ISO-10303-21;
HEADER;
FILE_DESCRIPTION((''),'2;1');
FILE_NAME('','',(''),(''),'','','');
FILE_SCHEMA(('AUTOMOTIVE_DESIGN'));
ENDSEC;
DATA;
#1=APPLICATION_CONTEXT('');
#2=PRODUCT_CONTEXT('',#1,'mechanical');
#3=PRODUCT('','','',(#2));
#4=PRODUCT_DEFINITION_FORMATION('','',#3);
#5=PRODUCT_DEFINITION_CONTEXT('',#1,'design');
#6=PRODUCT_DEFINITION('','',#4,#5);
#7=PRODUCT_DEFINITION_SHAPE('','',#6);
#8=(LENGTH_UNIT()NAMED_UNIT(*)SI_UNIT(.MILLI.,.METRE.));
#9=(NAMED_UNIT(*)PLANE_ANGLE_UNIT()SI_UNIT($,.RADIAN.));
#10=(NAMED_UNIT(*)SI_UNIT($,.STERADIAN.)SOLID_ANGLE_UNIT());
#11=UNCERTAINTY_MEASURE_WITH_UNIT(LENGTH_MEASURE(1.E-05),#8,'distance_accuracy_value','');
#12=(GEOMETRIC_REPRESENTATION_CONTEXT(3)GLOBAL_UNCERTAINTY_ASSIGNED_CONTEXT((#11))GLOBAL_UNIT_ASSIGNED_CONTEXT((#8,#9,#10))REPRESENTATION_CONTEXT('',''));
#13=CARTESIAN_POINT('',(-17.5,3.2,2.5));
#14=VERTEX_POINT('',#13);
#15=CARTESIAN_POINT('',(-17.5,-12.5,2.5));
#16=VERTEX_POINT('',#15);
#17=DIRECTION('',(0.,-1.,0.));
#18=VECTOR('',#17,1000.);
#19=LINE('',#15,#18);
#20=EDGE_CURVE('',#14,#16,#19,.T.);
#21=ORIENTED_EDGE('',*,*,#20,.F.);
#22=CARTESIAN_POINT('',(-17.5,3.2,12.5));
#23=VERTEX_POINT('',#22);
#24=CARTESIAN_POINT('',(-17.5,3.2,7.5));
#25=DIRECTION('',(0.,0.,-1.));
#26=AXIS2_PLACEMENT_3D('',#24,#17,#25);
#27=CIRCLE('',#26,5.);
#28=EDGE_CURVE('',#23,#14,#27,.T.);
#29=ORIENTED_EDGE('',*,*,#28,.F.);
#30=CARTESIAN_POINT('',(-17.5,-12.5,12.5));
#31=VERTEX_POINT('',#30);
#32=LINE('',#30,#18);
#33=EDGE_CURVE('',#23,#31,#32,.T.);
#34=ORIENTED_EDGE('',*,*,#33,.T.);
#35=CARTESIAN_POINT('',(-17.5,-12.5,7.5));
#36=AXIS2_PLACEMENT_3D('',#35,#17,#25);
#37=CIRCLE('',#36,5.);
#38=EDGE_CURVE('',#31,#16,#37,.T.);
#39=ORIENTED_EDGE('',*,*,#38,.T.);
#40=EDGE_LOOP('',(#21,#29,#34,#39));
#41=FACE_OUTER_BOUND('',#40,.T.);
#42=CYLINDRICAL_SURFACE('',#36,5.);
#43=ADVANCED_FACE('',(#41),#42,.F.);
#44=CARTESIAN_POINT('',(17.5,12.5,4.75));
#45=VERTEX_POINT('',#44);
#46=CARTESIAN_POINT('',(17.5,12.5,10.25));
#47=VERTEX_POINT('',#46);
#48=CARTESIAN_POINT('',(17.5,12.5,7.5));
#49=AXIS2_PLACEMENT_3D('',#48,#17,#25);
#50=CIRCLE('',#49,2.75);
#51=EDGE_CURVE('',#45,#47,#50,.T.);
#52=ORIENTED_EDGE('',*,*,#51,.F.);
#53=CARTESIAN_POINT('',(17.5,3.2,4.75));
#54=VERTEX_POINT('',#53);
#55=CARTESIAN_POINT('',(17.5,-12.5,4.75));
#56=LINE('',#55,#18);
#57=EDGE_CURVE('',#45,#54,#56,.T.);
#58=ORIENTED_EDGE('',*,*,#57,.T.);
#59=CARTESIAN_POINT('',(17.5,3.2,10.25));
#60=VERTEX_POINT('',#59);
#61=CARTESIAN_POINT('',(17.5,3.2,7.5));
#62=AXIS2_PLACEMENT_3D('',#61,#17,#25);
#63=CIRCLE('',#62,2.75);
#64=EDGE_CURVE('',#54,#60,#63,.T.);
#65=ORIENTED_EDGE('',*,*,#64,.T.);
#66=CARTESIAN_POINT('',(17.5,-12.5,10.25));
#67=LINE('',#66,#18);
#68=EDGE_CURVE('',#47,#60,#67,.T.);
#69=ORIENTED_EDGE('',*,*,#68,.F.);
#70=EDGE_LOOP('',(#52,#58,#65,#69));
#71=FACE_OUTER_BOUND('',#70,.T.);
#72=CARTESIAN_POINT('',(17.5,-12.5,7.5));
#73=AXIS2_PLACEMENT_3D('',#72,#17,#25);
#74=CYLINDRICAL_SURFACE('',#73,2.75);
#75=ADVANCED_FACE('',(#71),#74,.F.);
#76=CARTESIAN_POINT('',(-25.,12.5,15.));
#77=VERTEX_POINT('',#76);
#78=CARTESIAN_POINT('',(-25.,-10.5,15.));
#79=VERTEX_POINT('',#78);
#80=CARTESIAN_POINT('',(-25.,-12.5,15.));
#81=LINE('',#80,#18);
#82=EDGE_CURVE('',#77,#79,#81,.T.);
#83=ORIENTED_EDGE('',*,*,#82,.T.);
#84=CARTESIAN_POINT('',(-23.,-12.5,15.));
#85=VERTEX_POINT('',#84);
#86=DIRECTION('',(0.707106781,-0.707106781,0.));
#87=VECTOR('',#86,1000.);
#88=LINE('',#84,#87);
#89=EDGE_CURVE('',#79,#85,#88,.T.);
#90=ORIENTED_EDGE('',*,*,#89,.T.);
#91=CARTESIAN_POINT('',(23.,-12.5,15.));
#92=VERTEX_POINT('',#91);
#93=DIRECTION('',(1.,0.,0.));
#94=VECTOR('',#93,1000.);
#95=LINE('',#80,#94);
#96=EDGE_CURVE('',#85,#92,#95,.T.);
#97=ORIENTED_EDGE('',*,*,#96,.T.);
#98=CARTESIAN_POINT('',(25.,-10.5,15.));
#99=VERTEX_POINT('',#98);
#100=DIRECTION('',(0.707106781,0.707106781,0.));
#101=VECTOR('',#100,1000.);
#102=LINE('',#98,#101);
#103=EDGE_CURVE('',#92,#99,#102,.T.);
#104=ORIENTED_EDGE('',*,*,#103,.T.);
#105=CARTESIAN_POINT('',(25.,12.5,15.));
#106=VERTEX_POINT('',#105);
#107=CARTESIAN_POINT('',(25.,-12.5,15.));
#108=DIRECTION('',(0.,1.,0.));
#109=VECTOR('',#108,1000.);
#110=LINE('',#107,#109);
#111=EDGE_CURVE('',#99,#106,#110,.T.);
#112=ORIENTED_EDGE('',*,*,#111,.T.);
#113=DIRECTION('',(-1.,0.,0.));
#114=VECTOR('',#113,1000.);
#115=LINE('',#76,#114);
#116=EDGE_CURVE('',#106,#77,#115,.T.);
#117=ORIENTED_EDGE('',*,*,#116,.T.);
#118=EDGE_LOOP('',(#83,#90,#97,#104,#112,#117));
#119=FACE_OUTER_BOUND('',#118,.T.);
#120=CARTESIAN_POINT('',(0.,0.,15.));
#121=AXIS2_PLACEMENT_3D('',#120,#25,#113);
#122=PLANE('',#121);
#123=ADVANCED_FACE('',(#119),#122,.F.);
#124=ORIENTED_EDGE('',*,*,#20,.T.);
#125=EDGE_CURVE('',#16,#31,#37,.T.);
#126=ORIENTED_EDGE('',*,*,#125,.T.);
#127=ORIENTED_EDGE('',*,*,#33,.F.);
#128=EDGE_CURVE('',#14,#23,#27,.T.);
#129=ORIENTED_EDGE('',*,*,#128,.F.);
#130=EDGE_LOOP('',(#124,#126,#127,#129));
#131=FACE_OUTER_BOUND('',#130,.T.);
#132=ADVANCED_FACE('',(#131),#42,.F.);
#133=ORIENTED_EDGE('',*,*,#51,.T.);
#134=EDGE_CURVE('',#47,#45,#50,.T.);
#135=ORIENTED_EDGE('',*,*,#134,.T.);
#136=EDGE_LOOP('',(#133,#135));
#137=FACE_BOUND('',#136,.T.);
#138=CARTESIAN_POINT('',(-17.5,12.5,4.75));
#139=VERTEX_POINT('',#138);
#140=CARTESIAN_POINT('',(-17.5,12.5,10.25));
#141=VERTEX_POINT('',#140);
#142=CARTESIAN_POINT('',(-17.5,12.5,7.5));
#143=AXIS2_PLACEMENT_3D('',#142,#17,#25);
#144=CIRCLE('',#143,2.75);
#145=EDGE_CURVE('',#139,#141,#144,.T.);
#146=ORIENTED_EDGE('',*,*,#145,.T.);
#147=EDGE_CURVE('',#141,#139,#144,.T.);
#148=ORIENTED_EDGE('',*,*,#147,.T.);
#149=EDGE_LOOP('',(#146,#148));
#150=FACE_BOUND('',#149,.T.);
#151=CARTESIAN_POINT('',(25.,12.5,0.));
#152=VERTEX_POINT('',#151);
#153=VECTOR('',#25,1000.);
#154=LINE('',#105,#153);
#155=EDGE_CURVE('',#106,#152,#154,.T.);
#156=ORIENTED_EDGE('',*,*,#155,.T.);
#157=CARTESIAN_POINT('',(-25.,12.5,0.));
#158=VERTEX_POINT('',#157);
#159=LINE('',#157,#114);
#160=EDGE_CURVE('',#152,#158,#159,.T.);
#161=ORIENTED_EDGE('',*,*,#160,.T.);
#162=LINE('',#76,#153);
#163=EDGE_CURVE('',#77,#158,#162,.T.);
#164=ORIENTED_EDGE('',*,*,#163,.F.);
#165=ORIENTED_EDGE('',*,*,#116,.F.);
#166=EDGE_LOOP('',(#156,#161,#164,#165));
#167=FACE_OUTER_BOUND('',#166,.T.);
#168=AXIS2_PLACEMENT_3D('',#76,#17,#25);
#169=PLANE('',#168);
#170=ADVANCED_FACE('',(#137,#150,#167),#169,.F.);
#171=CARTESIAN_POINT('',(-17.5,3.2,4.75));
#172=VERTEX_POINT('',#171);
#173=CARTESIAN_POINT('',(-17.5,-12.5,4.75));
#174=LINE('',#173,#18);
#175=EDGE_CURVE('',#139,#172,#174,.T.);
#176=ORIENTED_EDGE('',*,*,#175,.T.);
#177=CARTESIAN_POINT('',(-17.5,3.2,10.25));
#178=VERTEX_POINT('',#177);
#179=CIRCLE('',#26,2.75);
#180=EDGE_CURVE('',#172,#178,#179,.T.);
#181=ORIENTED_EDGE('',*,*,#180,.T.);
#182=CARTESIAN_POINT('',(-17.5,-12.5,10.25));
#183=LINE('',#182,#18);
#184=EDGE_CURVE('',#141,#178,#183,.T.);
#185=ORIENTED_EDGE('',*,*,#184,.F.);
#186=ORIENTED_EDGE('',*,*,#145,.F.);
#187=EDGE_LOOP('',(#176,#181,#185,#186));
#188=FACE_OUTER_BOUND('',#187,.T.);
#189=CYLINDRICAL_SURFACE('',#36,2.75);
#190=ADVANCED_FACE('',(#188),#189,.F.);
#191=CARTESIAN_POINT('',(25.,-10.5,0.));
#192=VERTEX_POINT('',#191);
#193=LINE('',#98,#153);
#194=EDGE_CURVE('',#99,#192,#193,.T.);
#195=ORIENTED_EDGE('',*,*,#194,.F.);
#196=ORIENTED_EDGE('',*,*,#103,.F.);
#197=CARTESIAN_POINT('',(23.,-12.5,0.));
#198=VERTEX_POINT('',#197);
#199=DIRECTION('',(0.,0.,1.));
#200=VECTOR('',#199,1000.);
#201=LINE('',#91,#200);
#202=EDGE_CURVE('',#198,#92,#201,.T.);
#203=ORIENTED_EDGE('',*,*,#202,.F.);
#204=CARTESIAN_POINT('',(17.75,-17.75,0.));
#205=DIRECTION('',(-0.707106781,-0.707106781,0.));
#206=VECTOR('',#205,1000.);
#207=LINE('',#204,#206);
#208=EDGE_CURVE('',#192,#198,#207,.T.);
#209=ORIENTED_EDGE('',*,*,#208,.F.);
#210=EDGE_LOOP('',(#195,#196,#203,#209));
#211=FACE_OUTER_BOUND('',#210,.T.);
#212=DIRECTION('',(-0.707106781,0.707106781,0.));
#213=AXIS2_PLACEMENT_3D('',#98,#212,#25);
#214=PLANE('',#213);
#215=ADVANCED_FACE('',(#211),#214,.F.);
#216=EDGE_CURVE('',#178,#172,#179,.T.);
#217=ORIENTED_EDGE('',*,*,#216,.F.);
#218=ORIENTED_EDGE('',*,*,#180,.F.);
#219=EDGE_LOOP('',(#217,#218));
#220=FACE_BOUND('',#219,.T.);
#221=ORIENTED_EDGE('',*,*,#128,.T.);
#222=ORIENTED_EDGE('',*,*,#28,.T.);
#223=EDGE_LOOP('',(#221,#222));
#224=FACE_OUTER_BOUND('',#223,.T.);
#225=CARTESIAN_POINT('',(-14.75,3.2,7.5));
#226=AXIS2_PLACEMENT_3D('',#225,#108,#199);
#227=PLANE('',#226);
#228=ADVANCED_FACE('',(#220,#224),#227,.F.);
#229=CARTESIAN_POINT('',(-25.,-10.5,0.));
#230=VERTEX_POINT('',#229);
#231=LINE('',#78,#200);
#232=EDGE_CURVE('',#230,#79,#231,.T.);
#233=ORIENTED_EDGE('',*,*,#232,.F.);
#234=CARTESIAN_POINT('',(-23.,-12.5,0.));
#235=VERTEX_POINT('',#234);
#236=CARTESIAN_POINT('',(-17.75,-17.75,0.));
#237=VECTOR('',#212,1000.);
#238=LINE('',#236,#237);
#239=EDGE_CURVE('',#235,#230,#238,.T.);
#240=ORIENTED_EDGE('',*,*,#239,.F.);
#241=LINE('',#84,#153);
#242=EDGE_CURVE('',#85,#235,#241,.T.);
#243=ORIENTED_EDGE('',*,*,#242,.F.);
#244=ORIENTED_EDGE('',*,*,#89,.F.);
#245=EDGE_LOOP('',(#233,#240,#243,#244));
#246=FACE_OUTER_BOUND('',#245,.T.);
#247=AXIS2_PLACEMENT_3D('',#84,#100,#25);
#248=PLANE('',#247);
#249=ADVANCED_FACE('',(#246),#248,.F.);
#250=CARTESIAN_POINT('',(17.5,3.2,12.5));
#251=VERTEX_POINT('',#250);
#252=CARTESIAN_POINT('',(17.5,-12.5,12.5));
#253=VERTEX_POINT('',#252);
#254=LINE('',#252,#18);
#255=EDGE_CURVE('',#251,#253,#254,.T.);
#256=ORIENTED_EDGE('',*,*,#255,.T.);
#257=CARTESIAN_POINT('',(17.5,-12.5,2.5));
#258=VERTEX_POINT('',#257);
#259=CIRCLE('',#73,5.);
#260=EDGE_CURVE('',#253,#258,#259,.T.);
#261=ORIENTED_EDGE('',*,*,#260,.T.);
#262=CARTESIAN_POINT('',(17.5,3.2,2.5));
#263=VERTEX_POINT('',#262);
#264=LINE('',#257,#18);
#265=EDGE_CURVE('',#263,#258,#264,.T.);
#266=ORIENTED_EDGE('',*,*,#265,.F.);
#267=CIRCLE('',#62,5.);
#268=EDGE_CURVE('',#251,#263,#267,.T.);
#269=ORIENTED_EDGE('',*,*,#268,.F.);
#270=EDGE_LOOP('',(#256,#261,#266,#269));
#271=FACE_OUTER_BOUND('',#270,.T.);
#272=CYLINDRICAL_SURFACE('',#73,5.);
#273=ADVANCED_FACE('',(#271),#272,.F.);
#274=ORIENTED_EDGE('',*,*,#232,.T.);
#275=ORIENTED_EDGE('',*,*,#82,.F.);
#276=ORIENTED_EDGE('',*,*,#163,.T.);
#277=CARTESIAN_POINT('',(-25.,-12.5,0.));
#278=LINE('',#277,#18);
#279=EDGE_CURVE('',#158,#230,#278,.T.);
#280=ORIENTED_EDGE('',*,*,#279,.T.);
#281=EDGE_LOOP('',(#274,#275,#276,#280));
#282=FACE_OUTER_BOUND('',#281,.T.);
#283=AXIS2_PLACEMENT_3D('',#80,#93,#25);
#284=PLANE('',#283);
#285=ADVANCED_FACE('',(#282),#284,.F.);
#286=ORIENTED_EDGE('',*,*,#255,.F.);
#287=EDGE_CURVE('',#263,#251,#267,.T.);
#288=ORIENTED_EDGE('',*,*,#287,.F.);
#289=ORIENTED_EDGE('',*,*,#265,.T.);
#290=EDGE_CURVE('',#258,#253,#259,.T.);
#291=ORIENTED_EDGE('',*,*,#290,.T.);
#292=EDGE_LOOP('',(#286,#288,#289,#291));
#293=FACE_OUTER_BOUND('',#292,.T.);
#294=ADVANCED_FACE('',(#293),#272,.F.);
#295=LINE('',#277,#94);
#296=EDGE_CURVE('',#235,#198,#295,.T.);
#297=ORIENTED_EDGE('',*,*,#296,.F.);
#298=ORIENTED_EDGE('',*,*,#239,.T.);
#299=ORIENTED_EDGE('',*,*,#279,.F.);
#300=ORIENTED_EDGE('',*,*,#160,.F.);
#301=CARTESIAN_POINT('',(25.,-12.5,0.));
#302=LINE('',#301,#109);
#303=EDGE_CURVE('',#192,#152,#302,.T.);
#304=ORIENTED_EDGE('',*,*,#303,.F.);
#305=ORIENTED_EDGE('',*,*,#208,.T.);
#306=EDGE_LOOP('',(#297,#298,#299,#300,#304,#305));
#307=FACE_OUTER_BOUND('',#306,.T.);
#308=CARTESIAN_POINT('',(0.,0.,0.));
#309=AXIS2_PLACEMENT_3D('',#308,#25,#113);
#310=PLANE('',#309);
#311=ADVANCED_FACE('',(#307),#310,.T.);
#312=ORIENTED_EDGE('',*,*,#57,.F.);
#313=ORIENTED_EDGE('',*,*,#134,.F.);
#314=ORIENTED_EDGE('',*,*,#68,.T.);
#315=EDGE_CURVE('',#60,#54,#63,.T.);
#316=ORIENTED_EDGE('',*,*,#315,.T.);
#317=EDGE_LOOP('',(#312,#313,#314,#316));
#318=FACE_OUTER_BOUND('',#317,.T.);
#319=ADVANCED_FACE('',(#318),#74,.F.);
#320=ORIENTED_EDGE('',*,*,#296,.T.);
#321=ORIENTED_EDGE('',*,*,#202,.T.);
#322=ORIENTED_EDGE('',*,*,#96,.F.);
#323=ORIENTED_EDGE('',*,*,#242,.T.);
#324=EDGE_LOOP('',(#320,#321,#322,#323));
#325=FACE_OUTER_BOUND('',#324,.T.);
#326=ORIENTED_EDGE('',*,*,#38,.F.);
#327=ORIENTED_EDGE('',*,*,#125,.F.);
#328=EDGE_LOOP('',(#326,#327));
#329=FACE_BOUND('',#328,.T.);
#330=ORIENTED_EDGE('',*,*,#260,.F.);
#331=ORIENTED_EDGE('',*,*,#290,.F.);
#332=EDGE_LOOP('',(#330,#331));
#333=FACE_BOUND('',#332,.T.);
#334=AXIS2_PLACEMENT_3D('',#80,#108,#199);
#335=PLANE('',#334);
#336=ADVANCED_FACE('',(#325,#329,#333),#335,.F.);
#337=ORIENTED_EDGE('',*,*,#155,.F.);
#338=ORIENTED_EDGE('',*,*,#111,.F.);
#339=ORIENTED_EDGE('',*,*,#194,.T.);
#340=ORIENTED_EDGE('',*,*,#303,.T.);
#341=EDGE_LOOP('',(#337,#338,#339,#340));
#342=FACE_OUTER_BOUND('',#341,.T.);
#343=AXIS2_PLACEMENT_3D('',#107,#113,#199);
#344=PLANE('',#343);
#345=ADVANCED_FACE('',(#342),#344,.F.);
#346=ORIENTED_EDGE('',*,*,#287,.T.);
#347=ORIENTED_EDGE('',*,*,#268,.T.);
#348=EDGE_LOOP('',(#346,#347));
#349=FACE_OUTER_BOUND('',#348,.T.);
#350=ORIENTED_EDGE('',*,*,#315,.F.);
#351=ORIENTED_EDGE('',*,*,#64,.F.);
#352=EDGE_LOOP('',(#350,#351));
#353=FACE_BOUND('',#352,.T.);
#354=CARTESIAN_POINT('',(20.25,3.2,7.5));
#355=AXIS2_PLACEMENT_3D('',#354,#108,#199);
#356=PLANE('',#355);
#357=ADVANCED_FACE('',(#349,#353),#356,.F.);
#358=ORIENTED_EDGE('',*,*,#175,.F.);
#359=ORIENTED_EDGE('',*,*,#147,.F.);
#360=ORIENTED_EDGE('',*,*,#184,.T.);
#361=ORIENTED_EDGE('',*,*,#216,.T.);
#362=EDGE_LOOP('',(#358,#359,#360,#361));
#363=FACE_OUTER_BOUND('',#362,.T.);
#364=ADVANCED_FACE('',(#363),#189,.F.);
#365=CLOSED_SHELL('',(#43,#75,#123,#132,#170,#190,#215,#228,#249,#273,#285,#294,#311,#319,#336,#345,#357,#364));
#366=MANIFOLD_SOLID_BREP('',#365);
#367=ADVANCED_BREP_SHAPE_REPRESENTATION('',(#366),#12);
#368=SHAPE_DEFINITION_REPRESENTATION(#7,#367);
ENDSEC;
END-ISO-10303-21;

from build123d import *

# Parameters (mm, degrees)
SKETCH_1_W                   = 50
SKETCH_1_H                   = 25
EXTRUDE_1_DEPTH              = 15
CHAMFER_1_SIZE               = 2
HOLE_WIZARD_M5_1_D           = 5.5
HOLE_WIZARD_M5_1_CBORE_D     = 10
HOLE_WIZARD_M5_1_CBORE_DEPTH = 15.7


with BuildPart() as part:
    # 草图1 → 凸台-拉伸1 (new body)
    with BuildSketch(Plane.XY):
        Rectangle(SKETCH_1_W, SKETCH_1_H)
    extrude(amount=EXTRUDE_1_DEPTH)

    # 倒角1
    chamfer_1_edges = [part.edges().sort_by_distance(p)[0] for p in [
        (25, -12.5, 7.5),
        (-25, -12.5, 7.5),
    ]]
    chamfer(chamfer_1_edges, length=CHAMFER_1_SIZE)

    # M5 六角圆柱头螺钉的柱形沉头孔1 (through all)
    with Locations(Plane(origin=(0, -12.5, 0), x_dir=(-1, 0, 0), z_dir=(0, -1, 0))):
        with Locations((-17.5, -7.5), (17.5, -7.5)):
            CounterBoreHole(HOLE_WIZARD_M5_1_D / 2, HOLE_WIZARD_M5_1_CBORE_D / 2, HOLE_WIZARD_M5_1_CBORE_DEPTH)


solid = part.part
